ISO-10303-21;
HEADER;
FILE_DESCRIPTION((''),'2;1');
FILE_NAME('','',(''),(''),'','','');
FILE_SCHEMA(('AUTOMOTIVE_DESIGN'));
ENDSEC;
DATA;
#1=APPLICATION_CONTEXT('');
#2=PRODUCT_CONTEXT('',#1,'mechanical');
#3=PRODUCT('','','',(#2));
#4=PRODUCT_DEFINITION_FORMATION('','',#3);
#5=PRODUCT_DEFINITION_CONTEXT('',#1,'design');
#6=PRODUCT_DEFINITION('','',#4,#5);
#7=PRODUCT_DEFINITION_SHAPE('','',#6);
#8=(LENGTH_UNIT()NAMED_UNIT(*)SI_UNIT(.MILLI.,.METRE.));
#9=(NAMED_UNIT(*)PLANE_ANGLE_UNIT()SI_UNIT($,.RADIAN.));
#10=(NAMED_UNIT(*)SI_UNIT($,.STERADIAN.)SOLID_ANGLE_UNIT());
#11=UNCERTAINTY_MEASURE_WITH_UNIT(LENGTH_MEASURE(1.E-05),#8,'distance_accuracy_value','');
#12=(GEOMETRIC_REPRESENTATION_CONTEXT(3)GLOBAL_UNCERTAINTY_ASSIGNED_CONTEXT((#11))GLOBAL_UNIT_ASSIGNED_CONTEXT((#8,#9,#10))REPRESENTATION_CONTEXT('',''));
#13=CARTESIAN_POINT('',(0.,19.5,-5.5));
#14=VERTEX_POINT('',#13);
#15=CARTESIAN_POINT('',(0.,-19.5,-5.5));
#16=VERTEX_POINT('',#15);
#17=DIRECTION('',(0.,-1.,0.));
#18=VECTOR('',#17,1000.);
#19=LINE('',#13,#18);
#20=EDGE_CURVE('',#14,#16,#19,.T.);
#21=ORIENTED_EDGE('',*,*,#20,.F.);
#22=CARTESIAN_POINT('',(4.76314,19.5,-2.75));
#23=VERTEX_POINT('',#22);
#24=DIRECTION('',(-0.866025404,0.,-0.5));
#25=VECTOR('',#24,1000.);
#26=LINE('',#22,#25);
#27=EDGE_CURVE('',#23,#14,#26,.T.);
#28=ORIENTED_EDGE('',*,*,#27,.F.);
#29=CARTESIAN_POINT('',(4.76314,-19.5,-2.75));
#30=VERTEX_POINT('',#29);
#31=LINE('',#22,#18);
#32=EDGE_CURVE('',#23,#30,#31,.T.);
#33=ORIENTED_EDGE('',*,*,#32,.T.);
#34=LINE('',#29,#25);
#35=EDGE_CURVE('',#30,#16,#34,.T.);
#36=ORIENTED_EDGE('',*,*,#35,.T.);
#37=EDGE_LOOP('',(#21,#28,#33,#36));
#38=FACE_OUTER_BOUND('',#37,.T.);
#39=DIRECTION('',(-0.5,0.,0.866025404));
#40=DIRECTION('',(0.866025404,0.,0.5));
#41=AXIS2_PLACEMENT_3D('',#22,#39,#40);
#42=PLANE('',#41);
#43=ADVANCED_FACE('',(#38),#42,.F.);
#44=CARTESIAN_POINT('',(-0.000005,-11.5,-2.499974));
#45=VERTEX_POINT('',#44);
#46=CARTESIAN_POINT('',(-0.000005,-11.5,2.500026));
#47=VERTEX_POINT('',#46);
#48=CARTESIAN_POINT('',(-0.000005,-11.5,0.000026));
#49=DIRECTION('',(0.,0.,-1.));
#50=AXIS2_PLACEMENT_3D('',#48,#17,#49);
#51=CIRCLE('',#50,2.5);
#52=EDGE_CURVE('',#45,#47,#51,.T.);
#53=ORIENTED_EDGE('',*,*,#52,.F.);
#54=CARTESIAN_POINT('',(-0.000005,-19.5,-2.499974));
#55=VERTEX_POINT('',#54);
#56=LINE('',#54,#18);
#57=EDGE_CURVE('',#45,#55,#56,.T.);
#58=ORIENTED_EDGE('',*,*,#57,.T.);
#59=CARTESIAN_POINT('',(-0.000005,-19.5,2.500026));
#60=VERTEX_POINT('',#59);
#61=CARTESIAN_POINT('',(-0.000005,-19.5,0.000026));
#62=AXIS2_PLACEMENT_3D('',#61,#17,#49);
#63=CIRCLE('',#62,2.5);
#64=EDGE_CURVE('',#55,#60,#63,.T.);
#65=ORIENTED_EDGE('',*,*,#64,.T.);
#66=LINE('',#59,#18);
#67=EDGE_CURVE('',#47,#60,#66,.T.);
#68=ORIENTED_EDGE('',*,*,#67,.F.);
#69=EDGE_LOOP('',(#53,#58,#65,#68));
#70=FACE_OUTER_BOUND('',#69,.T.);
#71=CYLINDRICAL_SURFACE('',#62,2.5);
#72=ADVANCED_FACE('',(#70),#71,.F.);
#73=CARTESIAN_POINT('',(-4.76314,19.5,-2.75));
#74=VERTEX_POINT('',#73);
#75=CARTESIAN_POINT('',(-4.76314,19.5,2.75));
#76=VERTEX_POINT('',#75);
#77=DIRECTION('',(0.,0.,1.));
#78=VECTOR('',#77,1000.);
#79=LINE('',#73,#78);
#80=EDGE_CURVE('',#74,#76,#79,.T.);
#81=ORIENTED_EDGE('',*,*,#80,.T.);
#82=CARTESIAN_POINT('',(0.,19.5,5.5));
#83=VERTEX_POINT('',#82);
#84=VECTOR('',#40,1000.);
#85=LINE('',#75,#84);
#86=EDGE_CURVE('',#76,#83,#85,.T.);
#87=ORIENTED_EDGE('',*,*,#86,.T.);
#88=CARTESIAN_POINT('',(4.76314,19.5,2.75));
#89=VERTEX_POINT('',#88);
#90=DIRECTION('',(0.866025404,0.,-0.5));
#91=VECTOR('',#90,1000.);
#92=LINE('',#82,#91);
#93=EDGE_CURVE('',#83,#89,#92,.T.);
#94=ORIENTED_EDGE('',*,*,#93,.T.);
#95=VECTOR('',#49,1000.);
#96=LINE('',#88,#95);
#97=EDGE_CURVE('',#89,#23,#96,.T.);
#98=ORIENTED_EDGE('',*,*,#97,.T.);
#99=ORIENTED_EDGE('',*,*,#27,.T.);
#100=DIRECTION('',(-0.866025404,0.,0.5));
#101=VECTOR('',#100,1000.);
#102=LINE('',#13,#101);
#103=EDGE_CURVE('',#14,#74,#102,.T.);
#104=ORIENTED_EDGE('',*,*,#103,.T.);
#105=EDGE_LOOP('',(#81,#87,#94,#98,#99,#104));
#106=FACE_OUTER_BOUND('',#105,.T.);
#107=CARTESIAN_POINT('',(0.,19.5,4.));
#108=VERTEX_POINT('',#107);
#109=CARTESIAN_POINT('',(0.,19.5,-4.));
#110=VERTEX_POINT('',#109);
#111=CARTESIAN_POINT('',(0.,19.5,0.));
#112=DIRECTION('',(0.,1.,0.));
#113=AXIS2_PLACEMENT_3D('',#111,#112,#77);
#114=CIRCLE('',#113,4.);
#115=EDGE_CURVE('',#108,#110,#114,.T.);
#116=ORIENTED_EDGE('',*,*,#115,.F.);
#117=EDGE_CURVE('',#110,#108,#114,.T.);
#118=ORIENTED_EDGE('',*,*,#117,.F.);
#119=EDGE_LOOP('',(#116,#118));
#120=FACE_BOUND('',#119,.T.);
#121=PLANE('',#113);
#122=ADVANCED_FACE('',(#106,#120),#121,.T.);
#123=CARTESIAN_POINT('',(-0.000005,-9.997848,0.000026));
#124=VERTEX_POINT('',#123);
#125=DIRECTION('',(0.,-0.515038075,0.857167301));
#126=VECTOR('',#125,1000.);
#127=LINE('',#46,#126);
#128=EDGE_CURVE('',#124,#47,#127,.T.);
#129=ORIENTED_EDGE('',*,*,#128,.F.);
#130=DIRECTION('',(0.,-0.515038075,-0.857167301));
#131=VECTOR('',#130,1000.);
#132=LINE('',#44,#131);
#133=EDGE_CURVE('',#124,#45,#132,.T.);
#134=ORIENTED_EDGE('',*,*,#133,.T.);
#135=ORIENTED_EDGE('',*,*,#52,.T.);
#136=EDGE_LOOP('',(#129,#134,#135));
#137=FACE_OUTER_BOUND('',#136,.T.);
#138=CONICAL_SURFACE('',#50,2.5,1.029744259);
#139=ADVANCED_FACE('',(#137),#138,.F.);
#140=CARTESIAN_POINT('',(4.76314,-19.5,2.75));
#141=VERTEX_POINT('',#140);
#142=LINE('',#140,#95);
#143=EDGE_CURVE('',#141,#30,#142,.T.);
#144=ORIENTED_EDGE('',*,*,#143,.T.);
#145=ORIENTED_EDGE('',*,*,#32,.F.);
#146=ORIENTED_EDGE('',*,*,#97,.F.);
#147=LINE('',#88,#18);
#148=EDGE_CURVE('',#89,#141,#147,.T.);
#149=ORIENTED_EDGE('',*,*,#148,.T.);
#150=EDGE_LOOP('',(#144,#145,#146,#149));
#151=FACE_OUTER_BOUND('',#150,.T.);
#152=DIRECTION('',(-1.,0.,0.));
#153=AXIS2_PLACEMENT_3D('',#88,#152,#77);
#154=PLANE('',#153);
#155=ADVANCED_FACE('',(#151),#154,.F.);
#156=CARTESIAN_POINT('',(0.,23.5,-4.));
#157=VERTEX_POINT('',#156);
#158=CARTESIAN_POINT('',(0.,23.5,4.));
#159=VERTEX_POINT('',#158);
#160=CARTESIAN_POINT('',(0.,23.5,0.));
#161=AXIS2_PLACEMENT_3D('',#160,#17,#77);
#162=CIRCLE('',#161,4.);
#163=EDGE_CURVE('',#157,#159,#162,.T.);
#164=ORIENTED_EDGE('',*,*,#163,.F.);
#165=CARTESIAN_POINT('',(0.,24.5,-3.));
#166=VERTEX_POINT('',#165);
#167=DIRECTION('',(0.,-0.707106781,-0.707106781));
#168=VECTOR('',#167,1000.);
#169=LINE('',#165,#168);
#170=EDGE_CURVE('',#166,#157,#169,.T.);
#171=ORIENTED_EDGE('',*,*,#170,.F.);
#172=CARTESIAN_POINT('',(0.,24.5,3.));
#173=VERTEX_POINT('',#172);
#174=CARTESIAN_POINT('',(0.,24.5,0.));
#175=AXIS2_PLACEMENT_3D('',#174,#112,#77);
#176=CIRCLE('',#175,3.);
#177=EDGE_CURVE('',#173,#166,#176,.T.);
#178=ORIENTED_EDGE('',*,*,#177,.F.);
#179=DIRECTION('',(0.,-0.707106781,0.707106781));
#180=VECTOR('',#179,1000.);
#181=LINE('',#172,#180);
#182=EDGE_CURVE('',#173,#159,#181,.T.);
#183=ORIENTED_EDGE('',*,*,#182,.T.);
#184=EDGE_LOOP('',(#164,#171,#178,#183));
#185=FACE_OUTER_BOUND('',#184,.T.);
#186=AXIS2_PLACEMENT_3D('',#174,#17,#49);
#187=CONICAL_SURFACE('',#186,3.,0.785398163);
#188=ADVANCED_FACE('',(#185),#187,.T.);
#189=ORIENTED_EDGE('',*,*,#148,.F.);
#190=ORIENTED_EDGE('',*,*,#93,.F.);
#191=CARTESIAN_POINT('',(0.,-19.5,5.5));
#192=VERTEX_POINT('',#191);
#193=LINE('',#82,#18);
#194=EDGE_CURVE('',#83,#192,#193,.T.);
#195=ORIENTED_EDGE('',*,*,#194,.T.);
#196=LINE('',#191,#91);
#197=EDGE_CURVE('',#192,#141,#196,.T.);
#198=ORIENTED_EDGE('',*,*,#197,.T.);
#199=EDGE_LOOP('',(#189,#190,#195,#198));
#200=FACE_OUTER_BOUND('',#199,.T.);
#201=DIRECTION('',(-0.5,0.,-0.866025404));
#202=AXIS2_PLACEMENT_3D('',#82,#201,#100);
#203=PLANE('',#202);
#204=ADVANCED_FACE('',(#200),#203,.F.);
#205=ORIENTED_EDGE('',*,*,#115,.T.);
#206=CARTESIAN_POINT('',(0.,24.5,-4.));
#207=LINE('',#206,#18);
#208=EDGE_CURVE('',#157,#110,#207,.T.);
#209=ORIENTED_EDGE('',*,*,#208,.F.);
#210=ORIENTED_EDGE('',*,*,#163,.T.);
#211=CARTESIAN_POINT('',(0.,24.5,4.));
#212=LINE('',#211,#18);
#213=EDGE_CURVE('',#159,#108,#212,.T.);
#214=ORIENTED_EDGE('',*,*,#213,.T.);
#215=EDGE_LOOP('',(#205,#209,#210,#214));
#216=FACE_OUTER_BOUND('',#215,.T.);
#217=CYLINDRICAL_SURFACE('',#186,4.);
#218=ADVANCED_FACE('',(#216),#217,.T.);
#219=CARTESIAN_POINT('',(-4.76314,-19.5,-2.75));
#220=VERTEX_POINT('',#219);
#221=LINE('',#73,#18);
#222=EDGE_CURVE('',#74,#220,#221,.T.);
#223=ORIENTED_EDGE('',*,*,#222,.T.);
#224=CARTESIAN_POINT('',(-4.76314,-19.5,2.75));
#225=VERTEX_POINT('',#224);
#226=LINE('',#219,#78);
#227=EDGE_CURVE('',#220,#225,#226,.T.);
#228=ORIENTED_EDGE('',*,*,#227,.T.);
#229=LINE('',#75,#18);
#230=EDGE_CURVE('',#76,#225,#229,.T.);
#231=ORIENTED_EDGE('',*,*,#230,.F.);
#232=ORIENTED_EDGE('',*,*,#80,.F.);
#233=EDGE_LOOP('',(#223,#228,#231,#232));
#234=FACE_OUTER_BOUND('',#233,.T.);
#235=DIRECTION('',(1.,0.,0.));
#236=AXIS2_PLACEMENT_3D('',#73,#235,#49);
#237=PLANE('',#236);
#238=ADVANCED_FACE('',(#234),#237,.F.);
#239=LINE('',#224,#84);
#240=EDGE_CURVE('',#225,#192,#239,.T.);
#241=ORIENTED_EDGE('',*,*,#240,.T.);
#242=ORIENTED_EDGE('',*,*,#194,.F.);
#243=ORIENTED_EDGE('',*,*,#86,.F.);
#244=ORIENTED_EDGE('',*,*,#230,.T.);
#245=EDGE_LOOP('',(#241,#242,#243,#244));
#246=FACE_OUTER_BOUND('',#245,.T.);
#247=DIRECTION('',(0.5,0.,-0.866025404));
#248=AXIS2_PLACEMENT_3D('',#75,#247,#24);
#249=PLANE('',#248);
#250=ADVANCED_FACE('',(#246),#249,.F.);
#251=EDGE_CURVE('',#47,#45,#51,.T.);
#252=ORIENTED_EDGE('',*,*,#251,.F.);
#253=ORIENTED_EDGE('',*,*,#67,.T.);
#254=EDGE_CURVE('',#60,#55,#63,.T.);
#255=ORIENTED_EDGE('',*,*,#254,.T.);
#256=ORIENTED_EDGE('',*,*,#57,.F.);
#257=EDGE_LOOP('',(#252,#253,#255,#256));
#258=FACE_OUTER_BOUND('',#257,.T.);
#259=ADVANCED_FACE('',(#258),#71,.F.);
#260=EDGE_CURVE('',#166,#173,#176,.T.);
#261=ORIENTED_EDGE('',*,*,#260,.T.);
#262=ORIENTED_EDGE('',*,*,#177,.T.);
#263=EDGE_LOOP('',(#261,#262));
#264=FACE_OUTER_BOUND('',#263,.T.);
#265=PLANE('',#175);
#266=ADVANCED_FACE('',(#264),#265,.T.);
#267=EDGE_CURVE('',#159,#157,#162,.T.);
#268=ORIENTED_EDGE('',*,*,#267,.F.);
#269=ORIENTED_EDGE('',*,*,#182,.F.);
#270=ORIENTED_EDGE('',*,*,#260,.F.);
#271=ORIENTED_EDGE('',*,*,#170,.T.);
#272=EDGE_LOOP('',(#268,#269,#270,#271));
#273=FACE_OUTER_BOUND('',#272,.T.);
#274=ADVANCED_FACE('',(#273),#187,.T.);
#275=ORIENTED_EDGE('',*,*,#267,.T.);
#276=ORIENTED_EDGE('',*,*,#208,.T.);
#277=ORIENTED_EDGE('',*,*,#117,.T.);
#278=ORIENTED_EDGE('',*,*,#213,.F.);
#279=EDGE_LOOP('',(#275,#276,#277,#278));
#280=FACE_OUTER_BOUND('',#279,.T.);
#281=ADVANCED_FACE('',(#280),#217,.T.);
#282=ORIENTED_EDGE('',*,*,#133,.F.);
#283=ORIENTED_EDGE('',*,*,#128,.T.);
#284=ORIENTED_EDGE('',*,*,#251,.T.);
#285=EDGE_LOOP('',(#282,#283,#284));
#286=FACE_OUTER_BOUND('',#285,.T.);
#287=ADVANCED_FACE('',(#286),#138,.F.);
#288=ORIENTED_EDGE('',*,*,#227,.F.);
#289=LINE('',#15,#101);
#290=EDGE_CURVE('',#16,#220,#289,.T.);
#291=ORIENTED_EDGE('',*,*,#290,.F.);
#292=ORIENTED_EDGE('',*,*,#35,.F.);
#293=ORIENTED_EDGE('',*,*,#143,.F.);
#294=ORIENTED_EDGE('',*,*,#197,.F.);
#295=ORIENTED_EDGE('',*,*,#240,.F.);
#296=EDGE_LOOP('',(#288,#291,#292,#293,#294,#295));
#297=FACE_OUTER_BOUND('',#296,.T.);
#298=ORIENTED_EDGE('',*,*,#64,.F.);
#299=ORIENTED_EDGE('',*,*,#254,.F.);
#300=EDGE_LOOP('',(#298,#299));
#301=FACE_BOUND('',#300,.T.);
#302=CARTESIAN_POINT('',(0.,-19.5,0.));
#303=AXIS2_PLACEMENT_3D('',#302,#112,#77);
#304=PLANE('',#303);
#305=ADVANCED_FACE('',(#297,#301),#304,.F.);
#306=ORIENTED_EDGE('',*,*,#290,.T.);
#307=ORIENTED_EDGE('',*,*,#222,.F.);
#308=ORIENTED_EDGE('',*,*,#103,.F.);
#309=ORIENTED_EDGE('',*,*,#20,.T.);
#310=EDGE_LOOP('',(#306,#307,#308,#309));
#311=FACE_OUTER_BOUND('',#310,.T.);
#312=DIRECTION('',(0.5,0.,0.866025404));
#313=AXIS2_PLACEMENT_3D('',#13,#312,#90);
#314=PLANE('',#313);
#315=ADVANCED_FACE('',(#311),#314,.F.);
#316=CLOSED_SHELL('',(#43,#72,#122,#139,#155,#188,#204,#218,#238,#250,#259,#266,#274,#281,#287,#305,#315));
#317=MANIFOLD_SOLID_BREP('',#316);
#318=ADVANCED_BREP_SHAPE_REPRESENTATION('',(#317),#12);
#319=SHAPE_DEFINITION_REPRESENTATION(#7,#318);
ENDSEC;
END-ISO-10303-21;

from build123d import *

# Parameters (mm, degrees)
BOSS_EXTRUDE1_DEPTH = 19.5
SKETCH3_R           = 4
BOSS_EXTRUDE2_DEPTH = 5
CHAMFER1_SIZE       = 1


with BuildPart() as part:
    # Sketch1 → Boss-Extrude1 (new, symmetric)
    with BuildSketch(Plane(origin=(0, 0, 0), x_dir=(1, 0, 0), z_dir=(0, 1, 0))):
        Polygon((0, 5.5), (-4.763139721, 2.75), (-4.763139721, -2.75), (0, -5.5), (4.763139721, -2.75), (4.763139721, 2.75), align=None)
    extrude(amount=BOSS_EXTRUDE1_DEPTH, both=True)

    # Sketch3 → Boss-Extrude2 (add)
    with BuildSketch(Plane(origin=(0, 19.5, 0), x_dir=(1, 0, 0), z_dir=(0, 1, 0))):
        with Locations(Location((0, 0, 0), (0, 0, 270))):
            Circle(SKETCH3_R)
    extrude(amount=BOSS_EXTRUDE2_DEPTH)

    # Chamfer1
    chamfer1_edges = [part.edges().sort_by_distance(p)[0] for p in [
        (0, 24.5, -4),
    ]]
    chamfer(chamfer1_edges, length=CHAMFER1_SIZE)

    # Sketch6 → M6x1.0 Tapped Hole2 (revolve, cut)
    with BuildSketch(Plane(origin=(-4.548e-06, -19.5, 2.5825e-05), x_dir=(0, 0, -1), z_dir=(1, 0, 0))):
        Polygon((0, 0), (0, 9.502151548), (2.5, 8), (2.5, 0), align=None)
    revolve(axis=Axis((-4.548e-06, -25.85, 2.5825e-05), (0, 1, 0)), mode=Mode.SUBTRACT)


solid = part.part
